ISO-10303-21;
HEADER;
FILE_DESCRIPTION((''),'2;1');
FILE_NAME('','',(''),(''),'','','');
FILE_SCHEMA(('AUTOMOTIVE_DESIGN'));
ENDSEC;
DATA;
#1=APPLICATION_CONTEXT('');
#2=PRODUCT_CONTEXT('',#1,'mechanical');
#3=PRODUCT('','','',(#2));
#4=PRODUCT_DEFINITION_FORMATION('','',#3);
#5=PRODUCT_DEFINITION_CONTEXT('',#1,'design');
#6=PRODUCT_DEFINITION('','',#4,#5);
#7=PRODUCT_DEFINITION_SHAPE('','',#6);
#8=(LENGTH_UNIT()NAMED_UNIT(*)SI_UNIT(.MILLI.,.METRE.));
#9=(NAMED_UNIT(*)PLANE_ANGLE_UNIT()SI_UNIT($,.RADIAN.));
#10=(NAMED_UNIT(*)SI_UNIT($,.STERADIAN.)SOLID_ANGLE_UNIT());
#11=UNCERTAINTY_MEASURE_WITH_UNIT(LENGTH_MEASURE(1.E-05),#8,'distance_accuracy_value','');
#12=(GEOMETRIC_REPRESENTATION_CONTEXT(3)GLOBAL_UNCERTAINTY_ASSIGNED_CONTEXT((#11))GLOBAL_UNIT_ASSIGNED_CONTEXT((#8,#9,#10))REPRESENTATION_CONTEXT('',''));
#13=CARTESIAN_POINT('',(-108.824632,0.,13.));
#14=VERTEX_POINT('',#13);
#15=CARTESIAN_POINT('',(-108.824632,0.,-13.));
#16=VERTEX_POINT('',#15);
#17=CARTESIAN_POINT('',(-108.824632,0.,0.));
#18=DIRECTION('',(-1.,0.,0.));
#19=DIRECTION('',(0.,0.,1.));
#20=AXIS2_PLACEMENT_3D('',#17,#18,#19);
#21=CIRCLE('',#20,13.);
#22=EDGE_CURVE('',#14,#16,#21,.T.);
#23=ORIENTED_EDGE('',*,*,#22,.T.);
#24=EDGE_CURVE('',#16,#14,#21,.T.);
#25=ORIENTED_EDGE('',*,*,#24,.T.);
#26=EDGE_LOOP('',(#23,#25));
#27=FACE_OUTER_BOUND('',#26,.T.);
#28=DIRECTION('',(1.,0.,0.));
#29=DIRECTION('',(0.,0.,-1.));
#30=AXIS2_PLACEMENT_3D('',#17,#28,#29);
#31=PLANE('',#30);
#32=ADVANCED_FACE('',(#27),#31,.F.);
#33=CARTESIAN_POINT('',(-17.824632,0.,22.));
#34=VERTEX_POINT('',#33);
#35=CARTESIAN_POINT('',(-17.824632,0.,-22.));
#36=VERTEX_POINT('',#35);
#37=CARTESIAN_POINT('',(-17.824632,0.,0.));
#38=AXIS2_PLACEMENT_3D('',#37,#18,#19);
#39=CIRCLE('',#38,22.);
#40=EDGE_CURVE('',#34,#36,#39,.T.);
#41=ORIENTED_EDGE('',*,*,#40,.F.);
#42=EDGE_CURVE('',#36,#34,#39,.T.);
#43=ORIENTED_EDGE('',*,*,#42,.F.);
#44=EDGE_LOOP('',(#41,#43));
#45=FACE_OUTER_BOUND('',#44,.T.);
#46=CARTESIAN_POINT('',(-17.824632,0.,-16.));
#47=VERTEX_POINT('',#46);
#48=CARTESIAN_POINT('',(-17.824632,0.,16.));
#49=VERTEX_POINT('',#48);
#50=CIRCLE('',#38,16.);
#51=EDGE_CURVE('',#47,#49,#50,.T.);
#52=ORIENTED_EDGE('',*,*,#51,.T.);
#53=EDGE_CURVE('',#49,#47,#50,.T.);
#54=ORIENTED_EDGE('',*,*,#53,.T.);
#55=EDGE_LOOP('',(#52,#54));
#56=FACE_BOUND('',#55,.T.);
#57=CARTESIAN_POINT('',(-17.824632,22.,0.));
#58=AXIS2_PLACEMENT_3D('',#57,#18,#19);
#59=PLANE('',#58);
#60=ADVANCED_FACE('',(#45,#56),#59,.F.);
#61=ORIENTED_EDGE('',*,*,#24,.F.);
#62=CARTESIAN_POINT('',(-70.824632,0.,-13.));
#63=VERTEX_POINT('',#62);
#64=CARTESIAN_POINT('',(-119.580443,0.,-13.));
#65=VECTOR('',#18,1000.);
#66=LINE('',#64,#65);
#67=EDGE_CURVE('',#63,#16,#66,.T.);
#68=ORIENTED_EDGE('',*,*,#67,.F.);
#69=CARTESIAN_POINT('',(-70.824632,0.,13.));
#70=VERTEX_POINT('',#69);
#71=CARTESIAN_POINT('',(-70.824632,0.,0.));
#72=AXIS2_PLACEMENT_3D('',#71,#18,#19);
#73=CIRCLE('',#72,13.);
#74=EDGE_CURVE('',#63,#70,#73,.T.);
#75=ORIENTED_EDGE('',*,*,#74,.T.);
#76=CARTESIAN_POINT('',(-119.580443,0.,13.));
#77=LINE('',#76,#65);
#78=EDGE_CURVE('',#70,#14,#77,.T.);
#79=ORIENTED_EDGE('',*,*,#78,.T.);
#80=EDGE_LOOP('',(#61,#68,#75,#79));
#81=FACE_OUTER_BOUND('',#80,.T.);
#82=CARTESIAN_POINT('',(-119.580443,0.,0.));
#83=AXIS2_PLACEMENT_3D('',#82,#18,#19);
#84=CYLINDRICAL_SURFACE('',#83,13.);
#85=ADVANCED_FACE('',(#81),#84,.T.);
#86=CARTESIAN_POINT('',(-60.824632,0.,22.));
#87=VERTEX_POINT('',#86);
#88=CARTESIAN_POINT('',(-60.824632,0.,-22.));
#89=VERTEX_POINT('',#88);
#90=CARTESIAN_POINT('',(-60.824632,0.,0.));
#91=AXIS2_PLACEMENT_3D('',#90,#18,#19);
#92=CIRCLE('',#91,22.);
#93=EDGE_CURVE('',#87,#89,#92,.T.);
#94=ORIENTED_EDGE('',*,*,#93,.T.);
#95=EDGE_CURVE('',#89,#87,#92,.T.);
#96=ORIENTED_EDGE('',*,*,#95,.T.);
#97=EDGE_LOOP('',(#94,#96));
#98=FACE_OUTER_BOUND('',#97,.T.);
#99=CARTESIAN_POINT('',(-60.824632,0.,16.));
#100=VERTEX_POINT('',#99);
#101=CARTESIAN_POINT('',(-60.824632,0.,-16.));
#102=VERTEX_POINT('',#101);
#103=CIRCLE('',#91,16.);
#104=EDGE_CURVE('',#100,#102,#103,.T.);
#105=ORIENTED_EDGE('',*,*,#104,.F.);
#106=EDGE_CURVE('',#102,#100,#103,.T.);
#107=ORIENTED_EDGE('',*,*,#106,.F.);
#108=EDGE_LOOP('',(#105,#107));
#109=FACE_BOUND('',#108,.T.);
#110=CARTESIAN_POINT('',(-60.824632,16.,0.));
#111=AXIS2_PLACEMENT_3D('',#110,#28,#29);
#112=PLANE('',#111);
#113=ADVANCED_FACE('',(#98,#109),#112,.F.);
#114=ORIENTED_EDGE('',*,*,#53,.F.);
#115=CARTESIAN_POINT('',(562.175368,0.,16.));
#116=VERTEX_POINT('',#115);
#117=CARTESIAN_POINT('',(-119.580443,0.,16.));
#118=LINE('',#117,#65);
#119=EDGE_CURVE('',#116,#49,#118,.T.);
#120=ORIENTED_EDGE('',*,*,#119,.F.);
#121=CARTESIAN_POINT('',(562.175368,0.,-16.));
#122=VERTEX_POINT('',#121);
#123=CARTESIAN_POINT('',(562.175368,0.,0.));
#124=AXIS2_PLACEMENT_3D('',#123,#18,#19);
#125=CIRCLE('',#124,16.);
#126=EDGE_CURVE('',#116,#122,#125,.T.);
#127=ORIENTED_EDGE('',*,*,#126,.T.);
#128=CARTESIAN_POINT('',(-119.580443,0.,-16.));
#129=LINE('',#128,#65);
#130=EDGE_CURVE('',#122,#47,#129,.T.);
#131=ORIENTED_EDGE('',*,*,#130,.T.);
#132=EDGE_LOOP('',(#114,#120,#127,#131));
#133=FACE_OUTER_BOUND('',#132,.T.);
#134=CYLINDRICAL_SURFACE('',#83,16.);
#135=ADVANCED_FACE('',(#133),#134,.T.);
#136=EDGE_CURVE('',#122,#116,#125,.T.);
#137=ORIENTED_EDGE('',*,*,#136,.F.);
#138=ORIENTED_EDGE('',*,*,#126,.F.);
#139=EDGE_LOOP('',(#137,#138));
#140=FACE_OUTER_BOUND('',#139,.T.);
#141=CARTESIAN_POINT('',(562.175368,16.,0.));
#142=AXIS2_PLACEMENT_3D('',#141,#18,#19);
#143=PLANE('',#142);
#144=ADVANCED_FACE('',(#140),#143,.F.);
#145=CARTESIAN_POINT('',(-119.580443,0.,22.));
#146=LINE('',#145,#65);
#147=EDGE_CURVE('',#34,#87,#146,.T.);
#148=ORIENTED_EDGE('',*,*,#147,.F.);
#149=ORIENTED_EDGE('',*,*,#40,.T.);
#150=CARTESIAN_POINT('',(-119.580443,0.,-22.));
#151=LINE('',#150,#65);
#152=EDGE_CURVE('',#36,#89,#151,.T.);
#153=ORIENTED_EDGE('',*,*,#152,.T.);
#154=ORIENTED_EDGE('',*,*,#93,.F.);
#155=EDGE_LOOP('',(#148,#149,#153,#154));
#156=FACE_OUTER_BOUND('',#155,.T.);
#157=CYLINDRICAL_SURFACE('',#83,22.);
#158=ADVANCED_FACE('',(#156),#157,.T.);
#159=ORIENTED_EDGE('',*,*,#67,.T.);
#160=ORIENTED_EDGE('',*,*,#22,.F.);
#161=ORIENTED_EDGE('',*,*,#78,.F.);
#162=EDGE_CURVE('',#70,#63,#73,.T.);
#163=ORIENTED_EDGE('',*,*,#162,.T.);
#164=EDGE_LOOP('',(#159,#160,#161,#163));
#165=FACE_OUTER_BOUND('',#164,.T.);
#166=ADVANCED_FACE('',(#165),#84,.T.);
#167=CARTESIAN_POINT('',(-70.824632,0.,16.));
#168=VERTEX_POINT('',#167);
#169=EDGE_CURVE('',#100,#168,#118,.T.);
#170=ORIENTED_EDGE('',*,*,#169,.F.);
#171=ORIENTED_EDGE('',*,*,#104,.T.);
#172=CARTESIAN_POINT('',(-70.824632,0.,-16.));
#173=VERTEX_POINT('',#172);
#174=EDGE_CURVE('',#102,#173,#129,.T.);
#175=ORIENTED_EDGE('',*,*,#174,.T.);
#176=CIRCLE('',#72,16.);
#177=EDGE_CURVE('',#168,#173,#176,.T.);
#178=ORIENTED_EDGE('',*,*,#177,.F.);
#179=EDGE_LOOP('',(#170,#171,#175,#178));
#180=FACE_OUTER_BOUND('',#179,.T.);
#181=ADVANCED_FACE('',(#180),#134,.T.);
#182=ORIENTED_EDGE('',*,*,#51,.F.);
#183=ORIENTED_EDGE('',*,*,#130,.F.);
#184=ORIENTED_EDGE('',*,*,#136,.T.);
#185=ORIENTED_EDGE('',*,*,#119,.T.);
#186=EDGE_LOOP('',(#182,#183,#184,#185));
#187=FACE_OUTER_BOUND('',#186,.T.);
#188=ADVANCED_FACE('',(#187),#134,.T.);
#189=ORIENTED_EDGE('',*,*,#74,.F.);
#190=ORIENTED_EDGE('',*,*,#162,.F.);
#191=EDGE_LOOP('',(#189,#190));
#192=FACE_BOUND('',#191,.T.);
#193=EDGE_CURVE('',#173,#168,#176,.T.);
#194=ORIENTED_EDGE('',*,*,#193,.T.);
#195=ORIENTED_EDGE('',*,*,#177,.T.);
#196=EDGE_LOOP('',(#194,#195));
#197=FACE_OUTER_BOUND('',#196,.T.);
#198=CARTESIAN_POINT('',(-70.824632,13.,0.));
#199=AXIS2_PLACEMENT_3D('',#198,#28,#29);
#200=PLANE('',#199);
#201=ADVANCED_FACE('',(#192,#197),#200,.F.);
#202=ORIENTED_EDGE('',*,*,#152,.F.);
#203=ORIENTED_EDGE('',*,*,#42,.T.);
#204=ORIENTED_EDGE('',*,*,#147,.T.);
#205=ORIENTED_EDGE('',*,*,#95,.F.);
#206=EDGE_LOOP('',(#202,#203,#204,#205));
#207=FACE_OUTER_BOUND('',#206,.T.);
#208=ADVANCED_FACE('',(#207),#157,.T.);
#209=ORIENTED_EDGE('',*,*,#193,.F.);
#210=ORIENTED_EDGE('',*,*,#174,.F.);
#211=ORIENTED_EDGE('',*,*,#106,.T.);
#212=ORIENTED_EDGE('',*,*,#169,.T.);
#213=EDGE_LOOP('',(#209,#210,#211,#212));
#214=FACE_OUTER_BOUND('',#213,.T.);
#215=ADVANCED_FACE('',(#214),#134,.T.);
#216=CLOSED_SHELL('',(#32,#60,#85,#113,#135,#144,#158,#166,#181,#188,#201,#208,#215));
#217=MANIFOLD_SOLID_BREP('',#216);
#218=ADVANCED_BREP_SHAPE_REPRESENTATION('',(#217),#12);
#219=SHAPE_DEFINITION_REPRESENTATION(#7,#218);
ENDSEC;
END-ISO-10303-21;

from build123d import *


with BuildPart() as part:
    # 草图1 → 旋转1 (revolve)
    with BuildSketch(Plane.XY, mode=Mode.PRIVATE) as revolve_1_sk:
        Polygon((-108.824631792, 0), (-108.824631792, 13), (-70.824631792, 13), (-70.824631792, 16), (-60.824631792, 16), (-60.824631792, 22), (-17.824631792, 22), (-17.824631792, 16), (562.175368208, 16), (562.175368208, 0), align=None)
    revolve(revolve_1_sk.sketch.rotate(Axis((-119.580443242, 0, 0), (1, 0, 0)), 90), axis=Axis((-119.580443242, 0, 0), (1, 0, 0)))


solid = part.part
